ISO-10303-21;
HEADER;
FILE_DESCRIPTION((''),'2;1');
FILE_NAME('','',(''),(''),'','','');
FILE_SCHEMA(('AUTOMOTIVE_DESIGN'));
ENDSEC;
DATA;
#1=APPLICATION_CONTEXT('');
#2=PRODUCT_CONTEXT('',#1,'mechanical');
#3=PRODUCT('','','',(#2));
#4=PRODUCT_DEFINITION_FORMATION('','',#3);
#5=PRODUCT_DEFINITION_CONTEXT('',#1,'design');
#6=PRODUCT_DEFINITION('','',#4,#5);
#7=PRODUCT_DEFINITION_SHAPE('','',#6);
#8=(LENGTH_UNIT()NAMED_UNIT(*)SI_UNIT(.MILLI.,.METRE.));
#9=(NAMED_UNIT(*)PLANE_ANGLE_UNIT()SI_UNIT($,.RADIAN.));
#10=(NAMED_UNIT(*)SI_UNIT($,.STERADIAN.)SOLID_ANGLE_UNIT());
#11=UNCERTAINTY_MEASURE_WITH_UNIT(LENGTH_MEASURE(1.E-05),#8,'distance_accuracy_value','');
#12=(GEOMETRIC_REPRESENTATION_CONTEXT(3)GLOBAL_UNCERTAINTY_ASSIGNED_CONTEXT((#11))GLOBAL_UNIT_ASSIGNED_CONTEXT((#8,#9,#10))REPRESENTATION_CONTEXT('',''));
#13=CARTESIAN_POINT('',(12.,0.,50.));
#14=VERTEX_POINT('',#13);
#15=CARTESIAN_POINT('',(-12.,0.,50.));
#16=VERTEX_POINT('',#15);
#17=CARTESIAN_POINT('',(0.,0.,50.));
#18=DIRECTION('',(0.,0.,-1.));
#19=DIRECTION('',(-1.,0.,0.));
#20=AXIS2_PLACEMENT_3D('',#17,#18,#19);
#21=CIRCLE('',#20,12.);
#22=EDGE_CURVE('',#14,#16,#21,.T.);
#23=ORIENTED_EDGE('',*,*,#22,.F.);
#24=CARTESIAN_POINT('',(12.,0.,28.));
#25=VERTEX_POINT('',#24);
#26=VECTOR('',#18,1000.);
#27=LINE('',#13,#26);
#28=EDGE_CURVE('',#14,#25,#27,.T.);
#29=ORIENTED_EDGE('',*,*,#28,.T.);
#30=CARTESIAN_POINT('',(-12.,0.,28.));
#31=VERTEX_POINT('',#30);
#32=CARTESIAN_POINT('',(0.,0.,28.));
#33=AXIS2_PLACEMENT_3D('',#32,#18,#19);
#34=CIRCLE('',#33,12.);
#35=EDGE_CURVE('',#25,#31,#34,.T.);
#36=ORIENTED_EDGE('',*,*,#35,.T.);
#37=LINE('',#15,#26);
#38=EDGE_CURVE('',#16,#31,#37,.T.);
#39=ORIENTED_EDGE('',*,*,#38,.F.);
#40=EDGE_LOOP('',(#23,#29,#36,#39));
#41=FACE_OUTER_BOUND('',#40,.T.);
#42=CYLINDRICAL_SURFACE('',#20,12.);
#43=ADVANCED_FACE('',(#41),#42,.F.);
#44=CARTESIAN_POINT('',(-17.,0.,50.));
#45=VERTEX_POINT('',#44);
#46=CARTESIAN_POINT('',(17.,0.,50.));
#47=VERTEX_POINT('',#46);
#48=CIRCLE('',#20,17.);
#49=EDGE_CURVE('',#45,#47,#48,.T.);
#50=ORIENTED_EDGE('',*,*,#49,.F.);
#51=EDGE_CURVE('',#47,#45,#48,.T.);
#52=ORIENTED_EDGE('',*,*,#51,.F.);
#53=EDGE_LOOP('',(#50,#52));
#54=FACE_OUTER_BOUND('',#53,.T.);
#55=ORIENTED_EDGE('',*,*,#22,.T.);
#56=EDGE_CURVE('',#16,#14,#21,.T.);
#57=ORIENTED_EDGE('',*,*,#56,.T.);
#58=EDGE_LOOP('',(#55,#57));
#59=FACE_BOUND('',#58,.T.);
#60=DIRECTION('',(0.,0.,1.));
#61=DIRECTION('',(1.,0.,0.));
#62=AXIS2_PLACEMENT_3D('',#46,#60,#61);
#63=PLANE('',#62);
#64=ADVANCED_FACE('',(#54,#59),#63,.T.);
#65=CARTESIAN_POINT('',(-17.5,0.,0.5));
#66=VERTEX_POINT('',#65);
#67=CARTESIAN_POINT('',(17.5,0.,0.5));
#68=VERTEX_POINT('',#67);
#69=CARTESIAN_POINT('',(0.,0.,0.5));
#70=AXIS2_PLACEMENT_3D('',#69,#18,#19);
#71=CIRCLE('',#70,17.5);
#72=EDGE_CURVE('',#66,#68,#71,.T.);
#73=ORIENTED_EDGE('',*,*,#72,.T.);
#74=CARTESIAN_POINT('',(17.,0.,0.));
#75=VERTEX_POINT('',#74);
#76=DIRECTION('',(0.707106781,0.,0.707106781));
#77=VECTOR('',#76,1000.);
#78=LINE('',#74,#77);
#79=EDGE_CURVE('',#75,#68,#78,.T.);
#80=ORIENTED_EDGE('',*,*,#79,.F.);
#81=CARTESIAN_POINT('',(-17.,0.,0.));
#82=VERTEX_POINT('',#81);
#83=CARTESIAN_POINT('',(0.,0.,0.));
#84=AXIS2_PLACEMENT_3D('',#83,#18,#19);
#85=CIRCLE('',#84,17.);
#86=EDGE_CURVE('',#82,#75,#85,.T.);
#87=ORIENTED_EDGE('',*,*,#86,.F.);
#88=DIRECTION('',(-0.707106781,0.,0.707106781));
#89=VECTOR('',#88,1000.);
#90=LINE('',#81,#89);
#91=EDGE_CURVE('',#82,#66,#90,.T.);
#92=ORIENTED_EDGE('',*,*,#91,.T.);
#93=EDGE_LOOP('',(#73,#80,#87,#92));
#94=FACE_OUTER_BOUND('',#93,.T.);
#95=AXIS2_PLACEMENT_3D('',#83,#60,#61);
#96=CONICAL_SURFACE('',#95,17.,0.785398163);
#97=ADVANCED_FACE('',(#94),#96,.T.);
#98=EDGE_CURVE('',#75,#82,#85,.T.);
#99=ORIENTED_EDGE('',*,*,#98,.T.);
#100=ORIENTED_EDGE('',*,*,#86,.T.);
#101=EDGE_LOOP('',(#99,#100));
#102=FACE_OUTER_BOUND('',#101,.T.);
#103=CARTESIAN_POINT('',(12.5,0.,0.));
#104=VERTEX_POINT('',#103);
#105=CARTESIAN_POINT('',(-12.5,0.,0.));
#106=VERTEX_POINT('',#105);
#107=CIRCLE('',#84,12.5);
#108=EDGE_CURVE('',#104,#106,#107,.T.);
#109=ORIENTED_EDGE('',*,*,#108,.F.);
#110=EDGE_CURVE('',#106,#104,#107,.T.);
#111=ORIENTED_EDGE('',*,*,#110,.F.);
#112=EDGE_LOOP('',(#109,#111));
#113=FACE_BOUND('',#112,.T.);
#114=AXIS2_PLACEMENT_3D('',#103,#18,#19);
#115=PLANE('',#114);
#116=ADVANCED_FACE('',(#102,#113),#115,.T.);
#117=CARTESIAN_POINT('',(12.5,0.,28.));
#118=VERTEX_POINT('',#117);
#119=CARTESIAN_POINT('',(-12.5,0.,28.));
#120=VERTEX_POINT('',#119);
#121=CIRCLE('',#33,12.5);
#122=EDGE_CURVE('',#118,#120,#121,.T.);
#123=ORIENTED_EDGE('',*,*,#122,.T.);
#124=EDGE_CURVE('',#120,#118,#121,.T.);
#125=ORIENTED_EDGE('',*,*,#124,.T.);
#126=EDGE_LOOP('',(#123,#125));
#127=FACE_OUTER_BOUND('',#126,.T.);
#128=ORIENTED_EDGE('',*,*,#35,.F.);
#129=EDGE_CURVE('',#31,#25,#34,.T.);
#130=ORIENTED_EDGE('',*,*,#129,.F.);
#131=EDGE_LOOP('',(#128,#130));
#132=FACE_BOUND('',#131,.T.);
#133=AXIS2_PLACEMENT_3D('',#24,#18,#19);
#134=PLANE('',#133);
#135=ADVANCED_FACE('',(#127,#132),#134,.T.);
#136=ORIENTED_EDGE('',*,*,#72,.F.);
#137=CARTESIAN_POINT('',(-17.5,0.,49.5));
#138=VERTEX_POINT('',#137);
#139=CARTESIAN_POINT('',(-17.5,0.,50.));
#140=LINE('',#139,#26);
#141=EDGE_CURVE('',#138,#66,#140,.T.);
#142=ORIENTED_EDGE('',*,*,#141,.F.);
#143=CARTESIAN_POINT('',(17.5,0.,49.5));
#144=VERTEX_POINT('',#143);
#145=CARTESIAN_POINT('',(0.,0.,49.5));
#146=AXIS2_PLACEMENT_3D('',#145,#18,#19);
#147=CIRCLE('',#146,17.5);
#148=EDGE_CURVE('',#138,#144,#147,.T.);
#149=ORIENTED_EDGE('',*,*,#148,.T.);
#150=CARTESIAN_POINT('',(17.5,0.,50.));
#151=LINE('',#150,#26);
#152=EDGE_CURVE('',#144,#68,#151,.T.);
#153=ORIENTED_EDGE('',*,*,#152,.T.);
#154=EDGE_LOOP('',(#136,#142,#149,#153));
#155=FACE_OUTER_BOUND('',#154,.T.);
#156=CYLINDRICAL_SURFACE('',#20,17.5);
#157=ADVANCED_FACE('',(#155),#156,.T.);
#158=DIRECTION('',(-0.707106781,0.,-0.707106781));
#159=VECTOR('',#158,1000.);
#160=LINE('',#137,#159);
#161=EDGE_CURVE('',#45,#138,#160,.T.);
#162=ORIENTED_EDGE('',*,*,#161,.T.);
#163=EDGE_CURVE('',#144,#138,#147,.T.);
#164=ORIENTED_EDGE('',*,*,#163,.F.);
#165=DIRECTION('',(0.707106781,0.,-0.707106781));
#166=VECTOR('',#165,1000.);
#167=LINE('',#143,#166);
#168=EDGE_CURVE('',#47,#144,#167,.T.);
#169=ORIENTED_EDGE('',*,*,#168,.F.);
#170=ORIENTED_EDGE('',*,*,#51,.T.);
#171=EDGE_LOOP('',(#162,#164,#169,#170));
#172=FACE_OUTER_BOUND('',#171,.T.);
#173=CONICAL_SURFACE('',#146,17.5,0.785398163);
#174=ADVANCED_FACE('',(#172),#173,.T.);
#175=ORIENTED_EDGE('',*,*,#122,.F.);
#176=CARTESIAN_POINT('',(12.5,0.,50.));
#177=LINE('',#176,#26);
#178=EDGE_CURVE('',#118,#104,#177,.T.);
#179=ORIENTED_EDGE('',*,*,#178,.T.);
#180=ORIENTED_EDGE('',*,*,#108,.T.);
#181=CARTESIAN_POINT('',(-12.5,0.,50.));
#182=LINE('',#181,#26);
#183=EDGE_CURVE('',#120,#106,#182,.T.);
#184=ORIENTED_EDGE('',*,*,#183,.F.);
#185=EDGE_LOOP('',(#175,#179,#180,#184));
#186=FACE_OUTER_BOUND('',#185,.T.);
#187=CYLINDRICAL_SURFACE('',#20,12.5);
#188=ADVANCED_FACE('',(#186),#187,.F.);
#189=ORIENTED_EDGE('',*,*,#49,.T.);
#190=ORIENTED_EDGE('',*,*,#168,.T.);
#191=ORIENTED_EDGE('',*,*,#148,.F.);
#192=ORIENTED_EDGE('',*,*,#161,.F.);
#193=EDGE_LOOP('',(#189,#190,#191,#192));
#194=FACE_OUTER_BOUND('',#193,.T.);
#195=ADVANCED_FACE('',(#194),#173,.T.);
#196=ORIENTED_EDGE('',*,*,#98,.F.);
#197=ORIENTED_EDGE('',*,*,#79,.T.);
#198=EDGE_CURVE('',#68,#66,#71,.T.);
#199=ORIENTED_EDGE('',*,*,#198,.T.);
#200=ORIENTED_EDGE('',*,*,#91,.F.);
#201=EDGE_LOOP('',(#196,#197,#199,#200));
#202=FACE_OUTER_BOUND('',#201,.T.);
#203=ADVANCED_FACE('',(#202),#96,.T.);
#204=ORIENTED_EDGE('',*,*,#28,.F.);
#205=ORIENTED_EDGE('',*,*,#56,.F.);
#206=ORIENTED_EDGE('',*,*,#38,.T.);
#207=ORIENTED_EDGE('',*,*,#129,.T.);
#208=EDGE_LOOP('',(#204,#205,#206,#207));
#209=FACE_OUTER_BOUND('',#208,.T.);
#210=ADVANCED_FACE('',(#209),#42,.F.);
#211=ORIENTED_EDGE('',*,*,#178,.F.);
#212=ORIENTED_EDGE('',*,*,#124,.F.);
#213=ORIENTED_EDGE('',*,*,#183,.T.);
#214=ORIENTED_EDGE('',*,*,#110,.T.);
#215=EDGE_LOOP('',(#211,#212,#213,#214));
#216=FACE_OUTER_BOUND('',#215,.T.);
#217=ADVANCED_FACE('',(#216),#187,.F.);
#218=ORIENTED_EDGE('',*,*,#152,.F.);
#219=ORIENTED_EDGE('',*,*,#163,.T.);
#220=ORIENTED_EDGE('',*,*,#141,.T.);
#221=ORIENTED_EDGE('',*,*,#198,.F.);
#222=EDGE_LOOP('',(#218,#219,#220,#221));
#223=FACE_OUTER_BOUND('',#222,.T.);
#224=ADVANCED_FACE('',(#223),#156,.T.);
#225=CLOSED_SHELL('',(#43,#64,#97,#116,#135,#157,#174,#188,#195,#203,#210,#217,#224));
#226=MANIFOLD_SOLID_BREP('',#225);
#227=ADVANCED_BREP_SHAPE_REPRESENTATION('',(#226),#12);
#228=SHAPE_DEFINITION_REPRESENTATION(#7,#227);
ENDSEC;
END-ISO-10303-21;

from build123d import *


with BuildPart() as part:
    # Sketch1 → Revolve1 (revolve)
    with BuildSketch(Plane.XZ, mode=Mode.PRIVATE) as revolve1_sk:
        Polygon((12, 28), (12.5, 28), (12.5, 0), (17, 0), (17.5, 0.5), (17.5, 49.5), (17, 50), (12, 50), align=None)
    revolve(revolve1_sk.sketch.rotate(Axis((0, 0, 50), (0, 0, -1)), 180), axis=Axis((0, 0, 50), (0, 0, -1)))


solid = part.part
